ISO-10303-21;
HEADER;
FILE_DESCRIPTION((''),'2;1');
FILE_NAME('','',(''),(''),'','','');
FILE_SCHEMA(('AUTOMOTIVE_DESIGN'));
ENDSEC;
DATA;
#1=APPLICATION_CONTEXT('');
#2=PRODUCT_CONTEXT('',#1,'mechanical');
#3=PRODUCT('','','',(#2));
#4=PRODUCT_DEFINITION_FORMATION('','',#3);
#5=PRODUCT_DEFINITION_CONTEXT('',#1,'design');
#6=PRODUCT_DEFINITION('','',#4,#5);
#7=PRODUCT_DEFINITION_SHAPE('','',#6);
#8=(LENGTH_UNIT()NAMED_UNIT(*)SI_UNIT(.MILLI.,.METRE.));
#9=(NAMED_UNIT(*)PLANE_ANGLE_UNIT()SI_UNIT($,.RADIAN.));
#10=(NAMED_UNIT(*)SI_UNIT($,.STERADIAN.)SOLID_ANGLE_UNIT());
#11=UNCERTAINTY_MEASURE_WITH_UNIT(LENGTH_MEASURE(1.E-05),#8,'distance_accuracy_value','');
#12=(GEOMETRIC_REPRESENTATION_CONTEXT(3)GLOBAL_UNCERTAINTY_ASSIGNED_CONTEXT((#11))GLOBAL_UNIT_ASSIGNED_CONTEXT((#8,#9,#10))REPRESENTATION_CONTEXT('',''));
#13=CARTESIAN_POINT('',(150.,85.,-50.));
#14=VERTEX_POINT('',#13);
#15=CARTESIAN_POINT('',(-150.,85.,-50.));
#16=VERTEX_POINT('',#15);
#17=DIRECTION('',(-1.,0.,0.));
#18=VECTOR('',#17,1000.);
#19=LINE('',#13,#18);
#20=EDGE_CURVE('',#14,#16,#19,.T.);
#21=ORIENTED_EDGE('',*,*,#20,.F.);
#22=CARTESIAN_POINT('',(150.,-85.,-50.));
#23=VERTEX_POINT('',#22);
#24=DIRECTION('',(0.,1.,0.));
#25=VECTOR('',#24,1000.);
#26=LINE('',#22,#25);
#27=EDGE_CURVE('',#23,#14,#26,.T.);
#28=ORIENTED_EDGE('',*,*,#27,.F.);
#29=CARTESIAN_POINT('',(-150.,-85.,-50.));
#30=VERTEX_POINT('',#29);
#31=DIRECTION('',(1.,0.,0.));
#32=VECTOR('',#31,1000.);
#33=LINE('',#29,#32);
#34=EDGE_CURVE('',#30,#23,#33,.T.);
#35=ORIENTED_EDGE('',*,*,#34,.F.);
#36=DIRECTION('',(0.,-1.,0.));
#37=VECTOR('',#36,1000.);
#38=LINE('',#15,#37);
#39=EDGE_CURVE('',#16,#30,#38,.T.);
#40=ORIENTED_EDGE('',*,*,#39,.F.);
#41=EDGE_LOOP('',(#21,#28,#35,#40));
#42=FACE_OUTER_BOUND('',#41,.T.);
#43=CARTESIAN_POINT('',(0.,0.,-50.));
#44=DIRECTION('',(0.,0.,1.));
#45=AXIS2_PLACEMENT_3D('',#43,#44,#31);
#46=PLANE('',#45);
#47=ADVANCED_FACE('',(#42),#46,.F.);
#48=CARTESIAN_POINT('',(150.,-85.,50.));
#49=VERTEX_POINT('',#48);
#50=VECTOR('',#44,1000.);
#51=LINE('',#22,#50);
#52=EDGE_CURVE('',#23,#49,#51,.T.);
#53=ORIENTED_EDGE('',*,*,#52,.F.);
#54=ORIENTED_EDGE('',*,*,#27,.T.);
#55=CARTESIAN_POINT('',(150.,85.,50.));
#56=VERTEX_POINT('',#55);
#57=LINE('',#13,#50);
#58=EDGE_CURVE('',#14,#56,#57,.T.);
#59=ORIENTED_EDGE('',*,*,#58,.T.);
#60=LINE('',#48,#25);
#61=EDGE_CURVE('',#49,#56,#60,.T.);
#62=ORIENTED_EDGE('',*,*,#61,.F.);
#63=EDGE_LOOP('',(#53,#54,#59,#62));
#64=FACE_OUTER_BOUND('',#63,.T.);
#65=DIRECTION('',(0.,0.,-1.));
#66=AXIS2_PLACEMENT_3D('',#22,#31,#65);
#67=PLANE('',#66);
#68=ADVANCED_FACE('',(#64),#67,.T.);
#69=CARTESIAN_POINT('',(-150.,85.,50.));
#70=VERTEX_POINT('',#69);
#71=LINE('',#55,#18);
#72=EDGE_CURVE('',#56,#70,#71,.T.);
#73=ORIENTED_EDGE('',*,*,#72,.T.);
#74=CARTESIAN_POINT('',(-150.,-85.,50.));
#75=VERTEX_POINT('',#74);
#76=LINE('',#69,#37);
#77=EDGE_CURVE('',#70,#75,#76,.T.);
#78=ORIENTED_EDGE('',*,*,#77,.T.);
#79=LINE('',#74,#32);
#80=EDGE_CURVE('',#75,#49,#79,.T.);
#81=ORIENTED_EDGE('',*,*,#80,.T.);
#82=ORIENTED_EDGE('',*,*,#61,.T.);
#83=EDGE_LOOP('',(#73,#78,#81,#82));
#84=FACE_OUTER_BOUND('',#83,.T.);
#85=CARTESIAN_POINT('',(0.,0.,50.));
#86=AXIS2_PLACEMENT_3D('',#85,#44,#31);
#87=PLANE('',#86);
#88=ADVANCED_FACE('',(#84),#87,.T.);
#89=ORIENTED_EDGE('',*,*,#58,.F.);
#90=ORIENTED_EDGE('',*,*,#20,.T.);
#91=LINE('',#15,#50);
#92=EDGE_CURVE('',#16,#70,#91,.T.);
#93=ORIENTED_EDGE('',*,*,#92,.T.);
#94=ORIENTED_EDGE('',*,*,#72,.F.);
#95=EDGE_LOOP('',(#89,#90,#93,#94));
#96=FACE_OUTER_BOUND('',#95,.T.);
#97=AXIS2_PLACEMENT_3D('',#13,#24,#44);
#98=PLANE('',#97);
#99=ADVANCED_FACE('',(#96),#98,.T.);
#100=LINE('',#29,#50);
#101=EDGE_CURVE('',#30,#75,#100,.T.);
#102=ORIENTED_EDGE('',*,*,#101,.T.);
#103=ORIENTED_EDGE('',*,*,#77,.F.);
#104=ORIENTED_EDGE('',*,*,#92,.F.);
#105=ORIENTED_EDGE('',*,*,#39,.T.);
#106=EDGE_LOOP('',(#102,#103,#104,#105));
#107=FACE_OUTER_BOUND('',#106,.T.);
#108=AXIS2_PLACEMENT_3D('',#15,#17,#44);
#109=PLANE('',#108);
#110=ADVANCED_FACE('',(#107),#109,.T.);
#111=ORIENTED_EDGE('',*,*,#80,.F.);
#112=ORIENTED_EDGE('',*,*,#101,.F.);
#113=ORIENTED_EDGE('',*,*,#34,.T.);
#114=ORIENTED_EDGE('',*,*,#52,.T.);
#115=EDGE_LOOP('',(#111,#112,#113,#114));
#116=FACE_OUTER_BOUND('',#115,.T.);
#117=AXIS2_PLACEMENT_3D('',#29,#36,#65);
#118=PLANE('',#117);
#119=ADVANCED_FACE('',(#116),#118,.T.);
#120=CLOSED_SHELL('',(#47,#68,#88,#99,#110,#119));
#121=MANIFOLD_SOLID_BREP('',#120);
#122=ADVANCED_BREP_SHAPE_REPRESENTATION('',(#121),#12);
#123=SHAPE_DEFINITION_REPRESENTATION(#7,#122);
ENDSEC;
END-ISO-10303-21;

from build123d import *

# Parameters (mm, degrees)
SKETCH_1_W      = 300
SKETCH_1_H      = 170
EXTRUDE_1_DEPTH = 50


with BuildPart() as part:
    # 草图1 → 凸台-拉伸1 (new, symmetric)
    with BuildSketch(Plane.XY):
        Rectangle(SKETCH_1_W, SKETCH_1_H)
    extrude(amount=EXTRUDE_1_DEPTH, both=True)


solid = part.part
